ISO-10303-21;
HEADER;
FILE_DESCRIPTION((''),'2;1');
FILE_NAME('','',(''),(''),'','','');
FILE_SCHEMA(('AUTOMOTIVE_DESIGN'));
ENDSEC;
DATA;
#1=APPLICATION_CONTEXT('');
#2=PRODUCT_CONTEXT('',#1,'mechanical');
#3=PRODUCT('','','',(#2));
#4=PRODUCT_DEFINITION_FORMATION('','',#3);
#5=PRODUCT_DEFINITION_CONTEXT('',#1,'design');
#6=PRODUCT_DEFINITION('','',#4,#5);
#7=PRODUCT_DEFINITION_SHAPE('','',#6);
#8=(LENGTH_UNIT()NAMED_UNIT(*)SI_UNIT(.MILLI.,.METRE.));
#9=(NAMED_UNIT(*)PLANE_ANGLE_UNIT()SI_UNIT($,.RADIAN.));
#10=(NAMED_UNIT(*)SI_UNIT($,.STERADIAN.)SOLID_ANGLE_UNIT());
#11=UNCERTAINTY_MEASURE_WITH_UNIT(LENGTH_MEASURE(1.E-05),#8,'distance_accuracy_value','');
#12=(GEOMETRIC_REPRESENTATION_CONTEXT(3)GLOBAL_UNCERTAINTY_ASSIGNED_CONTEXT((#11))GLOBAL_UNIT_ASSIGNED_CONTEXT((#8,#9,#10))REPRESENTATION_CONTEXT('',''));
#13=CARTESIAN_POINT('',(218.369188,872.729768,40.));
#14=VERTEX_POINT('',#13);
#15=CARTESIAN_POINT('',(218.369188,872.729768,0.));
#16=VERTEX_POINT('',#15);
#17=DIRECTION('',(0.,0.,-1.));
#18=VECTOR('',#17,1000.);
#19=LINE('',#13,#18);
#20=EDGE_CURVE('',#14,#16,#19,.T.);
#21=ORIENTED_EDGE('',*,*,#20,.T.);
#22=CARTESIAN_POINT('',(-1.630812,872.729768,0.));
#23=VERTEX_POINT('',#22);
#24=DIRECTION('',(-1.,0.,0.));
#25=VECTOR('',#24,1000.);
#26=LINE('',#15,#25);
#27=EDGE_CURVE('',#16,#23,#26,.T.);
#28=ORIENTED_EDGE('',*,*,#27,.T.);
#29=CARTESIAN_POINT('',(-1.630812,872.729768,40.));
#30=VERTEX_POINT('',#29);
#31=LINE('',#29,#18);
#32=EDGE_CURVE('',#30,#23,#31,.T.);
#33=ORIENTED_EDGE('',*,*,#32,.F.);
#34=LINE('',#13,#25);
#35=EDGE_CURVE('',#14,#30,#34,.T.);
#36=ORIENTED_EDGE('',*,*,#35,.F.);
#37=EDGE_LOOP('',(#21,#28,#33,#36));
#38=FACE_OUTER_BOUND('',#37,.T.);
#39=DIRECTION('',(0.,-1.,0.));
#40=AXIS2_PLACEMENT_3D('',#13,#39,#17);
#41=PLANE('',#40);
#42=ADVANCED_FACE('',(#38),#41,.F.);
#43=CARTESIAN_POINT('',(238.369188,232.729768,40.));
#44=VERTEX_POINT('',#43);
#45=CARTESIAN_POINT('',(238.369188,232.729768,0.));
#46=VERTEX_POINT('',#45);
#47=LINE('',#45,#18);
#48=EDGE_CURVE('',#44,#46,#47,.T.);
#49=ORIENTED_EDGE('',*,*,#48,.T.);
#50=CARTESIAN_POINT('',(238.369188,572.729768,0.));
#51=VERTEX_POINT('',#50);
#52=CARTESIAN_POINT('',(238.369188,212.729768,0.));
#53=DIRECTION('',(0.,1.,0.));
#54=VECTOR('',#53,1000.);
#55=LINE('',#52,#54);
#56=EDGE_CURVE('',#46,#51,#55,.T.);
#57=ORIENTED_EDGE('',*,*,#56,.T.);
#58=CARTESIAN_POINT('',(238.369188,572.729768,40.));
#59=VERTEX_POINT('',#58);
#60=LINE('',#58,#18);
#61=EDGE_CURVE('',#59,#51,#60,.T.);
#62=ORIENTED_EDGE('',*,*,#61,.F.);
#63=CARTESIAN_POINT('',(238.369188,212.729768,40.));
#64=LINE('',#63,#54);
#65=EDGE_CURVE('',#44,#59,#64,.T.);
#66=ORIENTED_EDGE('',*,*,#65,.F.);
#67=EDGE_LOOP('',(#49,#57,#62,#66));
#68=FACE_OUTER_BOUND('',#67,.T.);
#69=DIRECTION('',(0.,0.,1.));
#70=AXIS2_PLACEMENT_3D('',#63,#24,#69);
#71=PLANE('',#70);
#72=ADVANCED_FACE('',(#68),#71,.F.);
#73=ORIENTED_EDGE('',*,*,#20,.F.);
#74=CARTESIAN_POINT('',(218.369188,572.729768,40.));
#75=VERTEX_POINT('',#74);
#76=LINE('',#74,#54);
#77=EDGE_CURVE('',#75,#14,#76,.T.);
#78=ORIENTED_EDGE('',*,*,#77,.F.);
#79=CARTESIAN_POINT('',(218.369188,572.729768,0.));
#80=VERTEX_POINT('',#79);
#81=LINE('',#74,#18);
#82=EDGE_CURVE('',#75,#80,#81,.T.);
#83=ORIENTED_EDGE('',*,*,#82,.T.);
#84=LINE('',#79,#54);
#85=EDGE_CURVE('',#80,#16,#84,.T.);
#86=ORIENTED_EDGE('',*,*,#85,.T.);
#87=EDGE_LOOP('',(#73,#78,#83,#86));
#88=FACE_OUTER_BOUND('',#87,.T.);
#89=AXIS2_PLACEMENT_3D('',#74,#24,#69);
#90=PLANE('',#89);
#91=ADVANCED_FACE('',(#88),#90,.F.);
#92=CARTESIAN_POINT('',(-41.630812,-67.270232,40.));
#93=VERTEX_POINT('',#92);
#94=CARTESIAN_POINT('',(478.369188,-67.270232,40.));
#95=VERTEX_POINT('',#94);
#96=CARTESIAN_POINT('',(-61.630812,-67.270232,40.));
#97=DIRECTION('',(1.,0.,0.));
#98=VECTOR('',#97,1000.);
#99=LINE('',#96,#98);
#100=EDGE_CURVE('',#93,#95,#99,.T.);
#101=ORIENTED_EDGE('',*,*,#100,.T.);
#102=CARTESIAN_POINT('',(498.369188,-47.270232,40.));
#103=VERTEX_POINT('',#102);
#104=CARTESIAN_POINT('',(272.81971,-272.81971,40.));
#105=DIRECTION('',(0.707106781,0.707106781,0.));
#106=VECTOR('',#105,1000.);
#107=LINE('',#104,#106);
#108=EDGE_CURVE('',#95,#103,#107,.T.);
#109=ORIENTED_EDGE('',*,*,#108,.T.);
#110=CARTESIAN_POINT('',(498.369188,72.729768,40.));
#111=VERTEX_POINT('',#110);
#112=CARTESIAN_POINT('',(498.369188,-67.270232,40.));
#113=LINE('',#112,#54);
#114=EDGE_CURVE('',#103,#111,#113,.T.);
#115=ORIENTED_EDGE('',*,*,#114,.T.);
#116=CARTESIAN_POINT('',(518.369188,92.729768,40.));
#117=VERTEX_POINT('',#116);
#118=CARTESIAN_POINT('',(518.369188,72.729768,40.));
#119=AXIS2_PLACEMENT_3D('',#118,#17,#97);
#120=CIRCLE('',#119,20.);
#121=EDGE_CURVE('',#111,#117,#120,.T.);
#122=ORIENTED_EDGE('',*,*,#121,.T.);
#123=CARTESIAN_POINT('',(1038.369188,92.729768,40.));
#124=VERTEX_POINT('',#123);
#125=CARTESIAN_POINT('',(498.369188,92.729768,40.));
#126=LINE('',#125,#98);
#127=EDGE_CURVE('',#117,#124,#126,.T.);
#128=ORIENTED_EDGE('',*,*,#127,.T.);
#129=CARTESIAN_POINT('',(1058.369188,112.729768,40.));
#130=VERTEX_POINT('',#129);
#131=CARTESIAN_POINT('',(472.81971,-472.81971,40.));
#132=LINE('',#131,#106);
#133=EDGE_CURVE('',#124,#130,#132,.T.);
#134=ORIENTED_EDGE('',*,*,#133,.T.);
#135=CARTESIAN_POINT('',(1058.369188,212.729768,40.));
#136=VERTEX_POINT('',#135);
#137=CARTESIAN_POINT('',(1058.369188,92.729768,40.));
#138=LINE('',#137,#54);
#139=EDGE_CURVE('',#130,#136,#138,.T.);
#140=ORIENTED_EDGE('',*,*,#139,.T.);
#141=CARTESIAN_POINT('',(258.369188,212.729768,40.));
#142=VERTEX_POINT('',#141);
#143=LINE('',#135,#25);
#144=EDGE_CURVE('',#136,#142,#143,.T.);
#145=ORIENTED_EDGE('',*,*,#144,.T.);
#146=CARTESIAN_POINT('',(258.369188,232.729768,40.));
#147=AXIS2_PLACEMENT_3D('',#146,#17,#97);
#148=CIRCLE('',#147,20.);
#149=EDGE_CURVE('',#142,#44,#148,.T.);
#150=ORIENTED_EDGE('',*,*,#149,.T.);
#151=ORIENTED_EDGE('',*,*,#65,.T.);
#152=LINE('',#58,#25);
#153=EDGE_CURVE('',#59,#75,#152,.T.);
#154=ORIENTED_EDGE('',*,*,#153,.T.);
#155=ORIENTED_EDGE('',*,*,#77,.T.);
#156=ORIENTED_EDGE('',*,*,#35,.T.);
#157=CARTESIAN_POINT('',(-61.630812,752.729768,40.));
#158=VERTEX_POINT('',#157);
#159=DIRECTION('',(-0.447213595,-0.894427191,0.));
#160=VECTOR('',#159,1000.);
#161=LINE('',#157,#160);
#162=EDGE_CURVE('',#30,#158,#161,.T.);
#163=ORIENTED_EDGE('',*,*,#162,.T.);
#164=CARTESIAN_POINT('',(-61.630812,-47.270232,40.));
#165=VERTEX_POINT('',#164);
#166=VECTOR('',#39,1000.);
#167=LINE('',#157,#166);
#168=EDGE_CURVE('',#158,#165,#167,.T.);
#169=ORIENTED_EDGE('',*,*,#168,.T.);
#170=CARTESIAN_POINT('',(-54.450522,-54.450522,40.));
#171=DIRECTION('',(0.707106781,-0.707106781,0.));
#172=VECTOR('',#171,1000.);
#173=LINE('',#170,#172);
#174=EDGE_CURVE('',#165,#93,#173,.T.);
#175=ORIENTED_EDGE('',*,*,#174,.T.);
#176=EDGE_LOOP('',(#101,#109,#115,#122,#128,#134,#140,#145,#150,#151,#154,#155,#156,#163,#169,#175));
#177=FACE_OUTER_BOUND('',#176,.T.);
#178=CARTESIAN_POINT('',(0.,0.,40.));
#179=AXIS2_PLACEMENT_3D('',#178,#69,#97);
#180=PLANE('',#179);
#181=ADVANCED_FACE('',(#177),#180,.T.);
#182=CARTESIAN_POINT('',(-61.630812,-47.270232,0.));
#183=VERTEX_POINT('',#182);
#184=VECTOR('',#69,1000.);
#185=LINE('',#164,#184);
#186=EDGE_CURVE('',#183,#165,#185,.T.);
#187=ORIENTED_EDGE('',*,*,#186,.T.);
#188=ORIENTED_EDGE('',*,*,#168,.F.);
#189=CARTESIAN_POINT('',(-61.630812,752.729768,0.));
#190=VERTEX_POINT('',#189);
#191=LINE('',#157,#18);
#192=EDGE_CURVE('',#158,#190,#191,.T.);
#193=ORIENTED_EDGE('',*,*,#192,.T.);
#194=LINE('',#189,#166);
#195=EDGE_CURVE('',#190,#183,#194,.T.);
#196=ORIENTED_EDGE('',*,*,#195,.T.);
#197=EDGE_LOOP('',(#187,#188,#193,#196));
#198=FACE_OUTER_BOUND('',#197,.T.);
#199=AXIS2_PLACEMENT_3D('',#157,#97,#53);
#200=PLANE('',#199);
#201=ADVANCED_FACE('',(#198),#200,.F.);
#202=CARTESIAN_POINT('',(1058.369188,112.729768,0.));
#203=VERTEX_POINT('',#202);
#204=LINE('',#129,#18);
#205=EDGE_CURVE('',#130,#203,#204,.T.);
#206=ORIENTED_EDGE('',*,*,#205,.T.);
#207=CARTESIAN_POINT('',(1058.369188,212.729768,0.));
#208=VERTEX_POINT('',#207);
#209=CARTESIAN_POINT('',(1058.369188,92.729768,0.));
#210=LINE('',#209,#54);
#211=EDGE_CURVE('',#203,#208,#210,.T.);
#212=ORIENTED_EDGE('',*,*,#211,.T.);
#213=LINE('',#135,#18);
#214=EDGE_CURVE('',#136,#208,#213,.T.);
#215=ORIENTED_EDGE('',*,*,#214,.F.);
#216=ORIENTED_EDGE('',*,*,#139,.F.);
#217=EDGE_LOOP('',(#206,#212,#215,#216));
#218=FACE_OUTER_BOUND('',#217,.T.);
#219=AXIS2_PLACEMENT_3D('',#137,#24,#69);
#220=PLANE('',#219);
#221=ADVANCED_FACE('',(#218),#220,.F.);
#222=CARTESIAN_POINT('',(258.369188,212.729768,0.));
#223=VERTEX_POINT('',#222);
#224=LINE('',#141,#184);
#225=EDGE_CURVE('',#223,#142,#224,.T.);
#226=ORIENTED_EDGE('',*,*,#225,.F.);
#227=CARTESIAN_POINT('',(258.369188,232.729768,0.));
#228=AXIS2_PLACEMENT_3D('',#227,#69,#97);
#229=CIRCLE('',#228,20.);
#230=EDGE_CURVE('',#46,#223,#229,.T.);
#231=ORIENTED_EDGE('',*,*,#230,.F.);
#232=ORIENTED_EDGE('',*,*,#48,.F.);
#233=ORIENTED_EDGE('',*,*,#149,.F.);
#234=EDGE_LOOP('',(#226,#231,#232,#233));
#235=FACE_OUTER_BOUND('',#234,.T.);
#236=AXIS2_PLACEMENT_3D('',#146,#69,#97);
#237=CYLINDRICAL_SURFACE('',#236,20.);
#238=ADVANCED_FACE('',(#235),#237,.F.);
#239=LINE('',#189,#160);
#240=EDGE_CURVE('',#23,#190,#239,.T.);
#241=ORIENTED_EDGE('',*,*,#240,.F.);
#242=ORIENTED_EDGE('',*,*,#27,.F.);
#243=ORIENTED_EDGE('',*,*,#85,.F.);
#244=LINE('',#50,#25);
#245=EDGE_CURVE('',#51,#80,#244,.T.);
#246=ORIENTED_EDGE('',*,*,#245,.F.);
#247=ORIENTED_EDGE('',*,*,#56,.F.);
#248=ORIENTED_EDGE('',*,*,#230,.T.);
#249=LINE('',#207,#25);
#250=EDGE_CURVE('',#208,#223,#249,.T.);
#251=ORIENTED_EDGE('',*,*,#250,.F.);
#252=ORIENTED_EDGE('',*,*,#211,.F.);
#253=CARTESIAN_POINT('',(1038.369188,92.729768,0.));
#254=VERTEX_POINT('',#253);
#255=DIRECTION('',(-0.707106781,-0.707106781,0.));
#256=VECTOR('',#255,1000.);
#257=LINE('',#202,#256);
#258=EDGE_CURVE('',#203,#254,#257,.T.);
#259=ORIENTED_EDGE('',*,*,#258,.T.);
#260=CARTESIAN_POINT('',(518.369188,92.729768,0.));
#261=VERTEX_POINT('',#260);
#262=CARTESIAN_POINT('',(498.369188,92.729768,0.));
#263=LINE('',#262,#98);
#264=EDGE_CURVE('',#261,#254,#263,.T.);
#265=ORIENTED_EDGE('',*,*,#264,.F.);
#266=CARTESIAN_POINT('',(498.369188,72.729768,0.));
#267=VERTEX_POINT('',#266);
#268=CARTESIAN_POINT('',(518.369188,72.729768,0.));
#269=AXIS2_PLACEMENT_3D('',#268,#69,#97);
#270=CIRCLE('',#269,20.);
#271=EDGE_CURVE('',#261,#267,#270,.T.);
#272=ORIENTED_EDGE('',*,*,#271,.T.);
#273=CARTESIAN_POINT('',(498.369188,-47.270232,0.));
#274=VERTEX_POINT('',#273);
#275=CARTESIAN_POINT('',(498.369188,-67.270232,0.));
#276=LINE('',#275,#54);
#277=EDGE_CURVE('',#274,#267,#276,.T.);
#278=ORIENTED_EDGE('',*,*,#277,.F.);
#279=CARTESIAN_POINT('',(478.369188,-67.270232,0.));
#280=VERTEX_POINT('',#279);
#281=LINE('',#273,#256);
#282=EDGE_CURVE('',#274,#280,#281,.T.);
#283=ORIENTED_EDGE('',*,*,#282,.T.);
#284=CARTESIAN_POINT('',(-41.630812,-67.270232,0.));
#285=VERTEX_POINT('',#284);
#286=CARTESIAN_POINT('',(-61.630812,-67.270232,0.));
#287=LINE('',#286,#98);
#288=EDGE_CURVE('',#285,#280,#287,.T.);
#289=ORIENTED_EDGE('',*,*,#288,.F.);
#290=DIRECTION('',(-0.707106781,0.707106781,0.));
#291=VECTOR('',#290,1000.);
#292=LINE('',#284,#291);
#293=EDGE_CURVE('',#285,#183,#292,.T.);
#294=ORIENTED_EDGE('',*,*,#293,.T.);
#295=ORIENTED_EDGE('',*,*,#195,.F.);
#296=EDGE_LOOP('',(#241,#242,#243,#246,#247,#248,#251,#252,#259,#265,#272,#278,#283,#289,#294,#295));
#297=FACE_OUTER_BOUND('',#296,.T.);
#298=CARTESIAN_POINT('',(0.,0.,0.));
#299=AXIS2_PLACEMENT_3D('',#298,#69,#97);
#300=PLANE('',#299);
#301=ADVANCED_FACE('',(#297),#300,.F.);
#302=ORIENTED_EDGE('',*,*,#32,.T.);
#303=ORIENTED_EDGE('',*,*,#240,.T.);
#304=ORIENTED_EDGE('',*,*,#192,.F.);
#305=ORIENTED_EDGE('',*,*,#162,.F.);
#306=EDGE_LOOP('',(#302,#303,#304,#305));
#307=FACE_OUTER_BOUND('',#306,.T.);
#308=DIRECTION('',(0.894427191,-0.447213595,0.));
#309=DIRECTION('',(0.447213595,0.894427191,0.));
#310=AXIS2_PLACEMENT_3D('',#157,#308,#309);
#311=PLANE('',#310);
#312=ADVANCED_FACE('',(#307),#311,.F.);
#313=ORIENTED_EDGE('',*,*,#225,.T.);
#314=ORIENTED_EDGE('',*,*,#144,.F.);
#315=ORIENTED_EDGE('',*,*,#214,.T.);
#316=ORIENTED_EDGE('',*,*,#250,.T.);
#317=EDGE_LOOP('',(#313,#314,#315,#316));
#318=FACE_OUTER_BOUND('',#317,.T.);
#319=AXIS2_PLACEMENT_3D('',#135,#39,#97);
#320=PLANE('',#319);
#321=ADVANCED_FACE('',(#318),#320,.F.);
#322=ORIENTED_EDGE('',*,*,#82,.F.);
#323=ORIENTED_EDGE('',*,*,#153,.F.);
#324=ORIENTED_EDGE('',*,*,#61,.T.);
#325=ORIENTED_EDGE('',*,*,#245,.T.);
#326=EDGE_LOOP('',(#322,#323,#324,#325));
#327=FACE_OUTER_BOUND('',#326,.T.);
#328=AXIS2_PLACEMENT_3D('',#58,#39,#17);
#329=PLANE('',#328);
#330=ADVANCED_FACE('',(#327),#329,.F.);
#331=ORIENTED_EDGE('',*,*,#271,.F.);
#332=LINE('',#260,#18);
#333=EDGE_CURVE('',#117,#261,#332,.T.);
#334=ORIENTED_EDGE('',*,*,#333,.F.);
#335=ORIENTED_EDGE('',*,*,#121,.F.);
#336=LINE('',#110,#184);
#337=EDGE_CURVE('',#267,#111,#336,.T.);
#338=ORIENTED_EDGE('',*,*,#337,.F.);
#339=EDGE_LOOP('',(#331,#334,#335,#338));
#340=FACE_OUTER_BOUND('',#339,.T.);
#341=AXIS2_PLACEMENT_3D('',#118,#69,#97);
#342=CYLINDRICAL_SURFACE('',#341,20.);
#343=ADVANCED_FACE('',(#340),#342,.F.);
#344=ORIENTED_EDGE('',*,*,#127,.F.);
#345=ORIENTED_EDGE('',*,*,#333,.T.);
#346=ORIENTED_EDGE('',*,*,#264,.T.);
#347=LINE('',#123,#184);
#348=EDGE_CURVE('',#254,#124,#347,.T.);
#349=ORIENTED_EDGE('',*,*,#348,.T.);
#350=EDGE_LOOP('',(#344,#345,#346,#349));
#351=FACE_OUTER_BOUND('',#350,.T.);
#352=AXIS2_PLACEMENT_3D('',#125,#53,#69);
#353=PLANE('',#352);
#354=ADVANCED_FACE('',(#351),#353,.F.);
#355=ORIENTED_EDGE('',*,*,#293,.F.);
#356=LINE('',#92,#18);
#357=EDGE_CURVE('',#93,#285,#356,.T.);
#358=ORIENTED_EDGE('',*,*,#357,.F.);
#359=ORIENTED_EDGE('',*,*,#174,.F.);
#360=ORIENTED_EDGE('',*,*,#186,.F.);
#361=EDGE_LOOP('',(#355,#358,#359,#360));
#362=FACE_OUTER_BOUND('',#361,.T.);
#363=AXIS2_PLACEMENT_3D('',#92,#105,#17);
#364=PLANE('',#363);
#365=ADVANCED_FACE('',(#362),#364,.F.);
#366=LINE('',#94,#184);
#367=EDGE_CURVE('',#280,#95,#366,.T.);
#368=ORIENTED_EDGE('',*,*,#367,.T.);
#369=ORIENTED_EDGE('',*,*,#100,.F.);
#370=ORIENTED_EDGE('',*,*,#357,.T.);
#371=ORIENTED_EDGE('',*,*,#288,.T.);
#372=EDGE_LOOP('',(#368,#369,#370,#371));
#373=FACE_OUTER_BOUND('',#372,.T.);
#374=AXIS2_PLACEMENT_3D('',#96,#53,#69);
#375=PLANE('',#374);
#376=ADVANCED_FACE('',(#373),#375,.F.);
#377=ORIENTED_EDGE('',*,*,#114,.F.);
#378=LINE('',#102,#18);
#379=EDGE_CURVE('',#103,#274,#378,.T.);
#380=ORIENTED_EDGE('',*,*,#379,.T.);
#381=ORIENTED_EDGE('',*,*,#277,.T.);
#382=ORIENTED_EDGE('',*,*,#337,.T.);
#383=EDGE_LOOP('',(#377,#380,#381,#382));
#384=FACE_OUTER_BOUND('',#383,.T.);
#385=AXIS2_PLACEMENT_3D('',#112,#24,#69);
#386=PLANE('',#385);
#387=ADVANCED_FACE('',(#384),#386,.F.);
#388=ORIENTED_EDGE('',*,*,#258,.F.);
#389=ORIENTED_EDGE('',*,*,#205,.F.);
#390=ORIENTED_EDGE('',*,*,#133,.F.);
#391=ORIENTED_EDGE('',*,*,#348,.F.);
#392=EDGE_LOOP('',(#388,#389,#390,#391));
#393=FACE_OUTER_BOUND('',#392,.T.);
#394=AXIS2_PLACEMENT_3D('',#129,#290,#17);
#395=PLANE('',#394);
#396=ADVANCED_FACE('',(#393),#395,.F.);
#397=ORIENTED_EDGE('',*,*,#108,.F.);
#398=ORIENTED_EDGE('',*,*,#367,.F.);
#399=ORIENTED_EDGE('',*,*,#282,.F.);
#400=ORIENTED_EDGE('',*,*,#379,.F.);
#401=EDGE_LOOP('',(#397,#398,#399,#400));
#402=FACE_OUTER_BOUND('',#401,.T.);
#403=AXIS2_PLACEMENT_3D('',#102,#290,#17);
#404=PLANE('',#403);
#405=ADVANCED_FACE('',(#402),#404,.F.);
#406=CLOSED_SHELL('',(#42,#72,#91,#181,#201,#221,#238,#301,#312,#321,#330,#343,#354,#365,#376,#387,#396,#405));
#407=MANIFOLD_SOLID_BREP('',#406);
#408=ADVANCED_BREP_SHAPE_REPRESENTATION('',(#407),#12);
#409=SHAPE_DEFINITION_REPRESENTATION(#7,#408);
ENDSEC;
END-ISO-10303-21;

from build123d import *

# Parameters (mm, degrees)
BOSS_EXTRUDE1_DEPTH = 40
CHAMFER1_SIZE       = 20
FILLET1_R           = 20


with BuildPart() as part:
    # Sketch1 → Boss-Extrude1 (new body)
    with BuildSketch(Plane.XY):
        Polygon((-61.630811554, 752.729767781), (-61.630811554, -67.270232219), (498.369188446, -67.270232219), (498.369188446, 92.729767781), (1058.369188446, 92.729767781), (1058.369188446, 212.729767781), (238.369188446, 212.729767781), (238.369188446, 572.729767781), (218.369188446, 572.729767781), (218.369188446, 872.729767781), (-1.630811554, 872.729767781), align=None)
    extrude(amount=BOSS_EXTRUDE1_DEPTH)

    # Chamfer1
    chamfer1_edges = [part.edges().sort_by_distance(p)[0] for p in [
        (-61.630811554, -67.270232219, 20),
        (1058.369188446, 92.729767781, 20),
        (498.369188446, -67.270232219, 20),
    ]]
    chamfer(chamfer1_edges, length=CHAMFER1_SIZE)

    # Fillet1
    fillet1_edges = [part.edges().sort_by_distance(p)[0] for p in [
        (238.369188446, 212.729767781, 20),
        (498.369188446, 92.729767781, 20),
    ]]
    fillet(fillet1_edges, radius=FILLET1_R)


solid = part.part
